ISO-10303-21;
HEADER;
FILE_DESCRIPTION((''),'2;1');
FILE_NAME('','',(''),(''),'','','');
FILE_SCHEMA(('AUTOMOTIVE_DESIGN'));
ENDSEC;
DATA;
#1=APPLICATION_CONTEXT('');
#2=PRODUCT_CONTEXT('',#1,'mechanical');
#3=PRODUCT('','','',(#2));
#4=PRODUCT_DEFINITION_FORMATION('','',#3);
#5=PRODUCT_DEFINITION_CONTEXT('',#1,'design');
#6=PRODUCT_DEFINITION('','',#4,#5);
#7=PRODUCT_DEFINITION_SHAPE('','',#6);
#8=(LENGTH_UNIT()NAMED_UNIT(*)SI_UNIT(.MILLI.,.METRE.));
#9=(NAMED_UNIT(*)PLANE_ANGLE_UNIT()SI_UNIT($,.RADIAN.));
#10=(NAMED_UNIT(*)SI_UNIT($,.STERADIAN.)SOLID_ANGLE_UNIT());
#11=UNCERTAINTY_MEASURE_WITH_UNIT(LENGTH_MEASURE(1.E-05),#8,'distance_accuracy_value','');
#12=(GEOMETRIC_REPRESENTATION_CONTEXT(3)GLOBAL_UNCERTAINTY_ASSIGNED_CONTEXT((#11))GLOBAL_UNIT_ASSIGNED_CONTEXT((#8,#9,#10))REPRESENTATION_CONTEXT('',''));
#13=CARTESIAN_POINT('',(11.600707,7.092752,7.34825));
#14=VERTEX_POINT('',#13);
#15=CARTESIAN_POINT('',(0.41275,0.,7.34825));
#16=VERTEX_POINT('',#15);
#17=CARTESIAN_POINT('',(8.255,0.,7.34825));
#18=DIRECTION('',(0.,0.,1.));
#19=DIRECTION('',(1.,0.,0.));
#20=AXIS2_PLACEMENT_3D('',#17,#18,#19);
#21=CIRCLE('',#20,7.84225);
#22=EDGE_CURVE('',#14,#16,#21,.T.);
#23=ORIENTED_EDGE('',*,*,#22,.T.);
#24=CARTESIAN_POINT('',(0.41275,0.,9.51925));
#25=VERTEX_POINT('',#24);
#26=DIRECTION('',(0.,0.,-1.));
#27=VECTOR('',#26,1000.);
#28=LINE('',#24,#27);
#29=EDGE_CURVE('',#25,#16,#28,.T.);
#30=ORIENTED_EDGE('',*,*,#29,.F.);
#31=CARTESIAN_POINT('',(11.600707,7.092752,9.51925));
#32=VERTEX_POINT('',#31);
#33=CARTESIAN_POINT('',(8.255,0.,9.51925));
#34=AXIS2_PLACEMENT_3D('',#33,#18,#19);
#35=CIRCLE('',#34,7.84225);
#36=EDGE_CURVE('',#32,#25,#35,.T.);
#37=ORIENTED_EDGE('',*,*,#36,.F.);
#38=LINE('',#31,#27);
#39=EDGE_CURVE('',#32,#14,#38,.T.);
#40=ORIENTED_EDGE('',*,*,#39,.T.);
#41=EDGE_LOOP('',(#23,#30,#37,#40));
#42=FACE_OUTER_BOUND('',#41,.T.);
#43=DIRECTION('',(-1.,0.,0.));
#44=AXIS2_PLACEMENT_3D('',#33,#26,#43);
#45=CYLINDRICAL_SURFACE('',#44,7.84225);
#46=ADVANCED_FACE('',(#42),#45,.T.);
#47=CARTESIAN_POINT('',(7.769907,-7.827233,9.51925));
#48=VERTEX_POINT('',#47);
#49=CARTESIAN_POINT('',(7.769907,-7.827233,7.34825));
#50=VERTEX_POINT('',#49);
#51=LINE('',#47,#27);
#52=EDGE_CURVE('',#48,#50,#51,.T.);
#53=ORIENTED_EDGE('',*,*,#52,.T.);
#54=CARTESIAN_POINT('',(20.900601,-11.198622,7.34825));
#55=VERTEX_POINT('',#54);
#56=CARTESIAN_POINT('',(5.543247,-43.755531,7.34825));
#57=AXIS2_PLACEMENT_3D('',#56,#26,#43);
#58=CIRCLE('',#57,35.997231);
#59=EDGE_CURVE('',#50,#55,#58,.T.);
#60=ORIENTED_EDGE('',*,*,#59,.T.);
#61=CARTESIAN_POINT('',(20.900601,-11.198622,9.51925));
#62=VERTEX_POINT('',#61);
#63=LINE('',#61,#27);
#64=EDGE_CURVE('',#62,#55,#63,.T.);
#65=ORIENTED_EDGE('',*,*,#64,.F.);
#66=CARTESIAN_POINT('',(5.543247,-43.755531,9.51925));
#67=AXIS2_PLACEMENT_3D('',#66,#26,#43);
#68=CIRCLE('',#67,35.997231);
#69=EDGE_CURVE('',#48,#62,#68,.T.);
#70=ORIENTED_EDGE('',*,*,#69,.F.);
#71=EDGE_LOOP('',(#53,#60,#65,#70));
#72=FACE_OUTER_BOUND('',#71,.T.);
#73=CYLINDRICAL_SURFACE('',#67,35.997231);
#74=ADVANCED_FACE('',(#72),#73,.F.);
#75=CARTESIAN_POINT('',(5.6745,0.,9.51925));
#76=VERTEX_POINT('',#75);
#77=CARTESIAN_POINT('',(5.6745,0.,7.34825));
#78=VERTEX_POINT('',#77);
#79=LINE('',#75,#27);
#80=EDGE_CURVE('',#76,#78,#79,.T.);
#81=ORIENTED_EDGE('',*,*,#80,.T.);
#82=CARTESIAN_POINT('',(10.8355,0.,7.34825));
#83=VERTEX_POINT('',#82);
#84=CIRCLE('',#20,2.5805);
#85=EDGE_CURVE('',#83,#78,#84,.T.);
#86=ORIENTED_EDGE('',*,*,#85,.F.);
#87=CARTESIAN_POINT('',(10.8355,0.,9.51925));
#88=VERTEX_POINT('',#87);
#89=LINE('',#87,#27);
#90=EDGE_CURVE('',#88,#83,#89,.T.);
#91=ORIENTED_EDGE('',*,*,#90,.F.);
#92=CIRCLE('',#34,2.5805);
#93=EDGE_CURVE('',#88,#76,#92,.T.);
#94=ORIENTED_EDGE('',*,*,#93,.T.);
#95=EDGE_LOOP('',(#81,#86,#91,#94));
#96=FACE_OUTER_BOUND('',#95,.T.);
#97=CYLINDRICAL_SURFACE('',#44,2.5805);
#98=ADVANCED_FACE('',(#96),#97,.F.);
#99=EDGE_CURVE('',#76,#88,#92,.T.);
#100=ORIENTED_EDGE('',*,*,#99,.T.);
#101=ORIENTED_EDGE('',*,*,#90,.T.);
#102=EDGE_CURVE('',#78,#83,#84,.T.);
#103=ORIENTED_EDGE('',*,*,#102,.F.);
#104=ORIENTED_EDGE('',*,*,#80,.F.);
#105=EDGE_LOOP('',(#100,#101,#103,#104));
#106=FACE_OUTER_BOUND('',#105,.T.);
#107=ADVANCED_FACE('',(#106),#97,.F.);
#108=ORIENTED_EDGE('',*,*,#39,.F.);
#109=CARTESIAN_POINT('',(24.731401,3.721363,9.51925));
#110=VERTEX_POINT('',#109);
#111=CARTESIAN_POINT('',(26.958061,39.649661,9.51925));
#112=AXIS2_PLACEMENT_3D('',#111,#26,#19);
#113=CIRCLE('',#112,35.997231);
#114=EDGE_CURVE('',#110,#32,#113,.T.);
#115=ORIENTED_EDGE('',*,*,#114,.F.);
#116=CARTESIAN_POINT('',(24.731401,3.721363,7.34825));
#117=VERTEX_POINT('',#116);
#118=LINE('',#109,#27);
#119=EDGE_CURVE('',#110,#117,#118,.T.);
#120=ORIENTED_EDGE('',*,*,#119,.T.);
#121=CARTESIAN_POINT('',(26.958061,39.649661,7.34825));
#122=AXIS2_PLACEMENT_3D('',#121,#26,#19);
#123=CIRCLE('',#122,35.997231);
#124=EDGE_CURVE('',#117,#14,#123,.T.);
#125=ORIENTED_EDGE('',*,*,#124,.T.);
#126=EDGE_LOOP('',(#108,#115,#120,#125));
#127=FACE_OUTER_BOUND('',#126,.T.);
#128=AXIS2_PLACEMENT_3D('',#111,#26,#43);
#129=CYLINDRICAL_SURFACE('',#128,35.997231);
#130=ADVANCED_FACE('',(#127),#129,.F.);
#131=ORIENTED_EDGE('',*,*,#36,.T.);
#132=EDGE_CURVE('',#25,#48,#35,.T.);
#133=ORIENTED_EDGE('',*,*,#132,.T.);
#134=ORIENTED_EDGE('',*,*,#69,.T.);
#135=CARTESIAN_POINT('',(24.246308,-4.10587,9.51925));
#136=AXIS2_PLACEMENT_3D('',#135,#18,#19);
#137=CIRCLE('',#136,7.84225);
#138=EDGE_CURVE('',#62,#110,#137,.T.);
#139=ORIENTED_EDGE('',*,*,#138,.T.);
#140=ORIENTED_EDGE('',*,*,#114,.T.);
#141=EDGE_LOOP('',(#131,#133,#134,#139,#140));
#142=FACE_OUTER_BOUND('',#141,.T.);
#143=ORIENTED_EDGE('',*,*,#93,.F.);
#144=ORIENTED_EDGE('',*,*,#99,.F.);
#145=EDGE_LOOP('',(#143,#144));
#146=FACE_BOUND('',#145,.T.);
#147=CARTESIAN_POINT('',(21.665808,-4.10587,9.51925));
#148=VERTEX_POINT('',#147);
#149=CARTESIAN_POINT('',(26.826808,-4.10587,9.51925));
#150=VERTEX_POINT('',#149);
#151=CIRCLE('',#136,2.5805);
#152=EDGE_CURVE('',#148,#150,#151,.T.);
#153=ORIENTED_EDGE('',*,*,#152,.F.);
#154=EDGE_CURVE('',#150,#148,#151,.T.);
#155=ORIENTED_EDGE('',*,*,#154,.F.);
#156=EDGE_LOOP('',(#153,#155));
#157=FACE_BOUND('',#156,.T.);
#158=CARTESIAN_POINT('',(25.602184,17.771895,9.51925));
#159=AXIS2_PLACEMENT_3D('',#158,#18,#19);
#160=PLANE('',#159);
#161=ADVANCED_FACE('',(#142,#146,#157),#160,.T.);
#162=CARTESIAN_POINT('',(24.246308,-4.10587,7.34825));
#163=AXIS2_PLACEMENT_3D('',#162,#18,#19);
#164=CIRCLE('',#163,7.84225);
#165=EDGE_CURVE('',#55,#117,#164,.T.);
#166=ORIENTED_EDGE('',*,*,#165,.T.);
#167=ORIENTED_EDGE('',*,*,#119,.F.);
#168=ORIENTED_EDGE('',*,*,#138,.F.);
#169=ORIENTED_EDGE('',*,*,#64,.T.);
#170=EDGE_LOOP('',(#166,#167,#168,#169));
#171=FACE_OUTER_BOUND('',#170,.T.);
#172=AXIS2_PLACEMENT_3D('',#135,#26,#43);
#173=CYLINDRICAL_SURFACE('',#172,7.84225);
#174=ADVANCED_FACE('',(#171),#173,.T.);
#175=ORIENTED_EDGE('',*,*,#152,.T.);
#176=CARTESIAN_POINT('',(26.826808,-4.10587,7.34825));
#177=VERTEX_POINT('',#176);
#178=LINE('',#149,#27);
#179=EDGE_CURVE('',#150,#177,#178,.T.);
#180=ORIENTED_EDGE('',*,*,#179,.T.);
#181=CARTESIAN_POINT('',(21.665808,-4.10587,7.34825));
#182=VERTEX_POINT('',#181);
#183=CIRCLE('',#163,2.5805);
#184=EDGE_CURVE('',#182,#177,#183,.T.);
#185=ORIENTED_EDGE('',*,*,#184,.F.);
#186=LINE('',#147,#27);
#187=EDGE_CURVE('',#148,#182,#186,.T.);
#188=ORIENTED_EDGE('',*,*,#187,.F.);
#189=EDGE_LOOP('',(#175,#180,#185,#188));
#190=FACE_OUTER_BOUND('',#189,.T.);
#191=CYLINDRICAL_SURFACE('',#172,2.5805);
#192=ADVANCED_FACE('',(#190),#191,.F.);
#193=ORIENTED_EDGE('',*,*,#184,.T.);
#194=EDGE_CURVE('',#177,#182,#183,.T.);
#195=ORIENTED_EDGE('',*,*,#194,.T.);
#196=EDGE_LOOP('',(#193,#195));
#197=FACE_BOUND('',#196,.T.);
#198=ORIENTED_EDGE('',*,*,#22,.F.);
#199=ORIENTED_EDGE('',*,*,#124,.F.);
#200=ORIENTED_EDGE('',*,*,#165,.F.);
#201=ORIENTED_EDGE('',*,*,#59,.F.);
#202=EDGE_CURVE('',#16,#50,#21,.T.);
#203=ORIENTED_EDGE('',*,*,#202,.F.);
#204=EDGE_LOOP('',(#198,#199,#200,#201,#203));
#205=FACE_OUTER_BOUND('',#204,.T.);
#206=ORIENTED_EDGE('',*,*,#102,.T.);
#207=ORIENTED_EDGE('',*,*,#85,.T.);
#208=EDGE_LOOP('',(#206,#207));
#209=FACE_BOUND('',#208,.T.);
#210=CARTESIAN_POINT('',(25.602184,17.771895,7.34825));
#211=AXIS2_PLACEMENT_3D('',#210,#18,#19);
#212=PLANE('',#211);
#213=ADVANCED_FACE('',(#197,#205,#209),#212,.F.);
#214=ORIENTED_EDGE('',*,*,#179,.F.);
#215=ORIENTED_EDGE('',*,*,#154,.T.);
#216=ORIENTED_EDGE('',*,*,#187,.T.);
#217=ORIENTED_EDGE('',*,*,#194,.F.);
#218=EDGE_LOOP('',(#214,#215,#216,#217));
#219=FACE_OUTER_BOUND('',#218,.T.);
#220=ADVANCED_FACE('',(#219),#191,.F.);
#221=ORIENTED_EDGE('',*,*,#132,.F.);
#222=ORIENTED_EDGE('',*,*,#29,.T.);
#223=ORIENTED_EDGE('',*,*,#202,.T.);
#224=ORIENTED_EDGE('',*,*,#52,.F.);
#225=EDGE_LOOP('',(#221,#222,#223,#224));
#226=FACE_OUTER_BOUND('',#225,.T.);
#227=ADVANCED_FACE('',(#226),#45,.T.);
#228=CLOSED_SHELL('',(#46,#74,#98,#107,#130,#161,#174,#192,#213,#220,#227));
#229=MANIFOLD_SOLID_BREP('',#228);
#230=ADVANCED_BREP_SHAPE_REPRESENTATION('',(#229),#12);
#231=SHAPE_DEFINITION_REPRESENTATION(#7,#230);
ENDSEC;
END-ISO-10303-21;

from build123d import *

# Parameters (mm, degrees)
SKETCH_2_R        = 7.94
EXTRUDE_1_DEPTH   = 7.875
EXTRUDE_1_2_DEPTH = 7.875
EXTRUDE_2_DEPTH   = 3.43
SKETCH_6_R        = 3.97
EXTRUDE_4_DEPTH   = 3.34
SCALE_1_SCALE     = 0.65


with BuildPart() as part:
    # 草图2 → 拉伸1 (new, symmetric)
    with BuildSketch(Plane.XY):
        with Locations((12.7, 0)):
            Circle(SKETCH_2_R)
    extrude(amount=EXTRUDE_1_DEPTH, both=True)



with BuildPart() as body_2:
    # 草图2 → Extrude 1 2 (new, symmetric)
    with BuildSketch(Plane.XY):
        with Locations((-12.7, 0)):
            Circle(SKETCH_2_R)
    extrude(amount=EXTRUDE_1_2_DEPTH, both=True)


with BuildPart() as part_1:
    add(part.part)

    add(body_2.part)  # 拉伸2 merges body 2
    # 草图3 → 拉伸2 (add)
    with BuildSketch(Plane.XY.offset(7.875)):
        with BuildLine():
            ThreePointArc((-10.428153415, 11.849174574), (-24.765, 0), (-10.428153415, -11.849174574))
            ThreePointArc((-10.428153415, -11.849174574), (0, -10.8585), (10.428153415, -11.849174574))
            ThreePointArc((10.428153415, -11.849174574), (24.765, 0), (10.428153415, 11.849174574))
            ThreePointArc((10.428153415, 11.849174574), (0, 10.8585), (-10.428153415, 11.849174574))
        make_face()
    extrude(amount=EXTRUDE_2_DEPTH)


with BuildPart() as body_2_2:
    # 草图6 → 拉伸4 (new body)
    with BuildSketch(Plane.XY.offset(11.305)):
        with BuildLine():
            ThreePointArc((32.154770058, -17.228648829), (48.987968132, -9.317166623), (38.048309834, 5.725173103))
            ThreePointArc((38.048309834, 5.725173103), (27.701405286, 7.358998688), (17.847242234, 10.911925695))
            ThreePointArc((17.847242234, 10.911925695), (1.014044161, 3.000443489), (11.953702459, -12.041896237))
            ThreePointArc((11.953702459, -12.041896237), (22.300607007, -13.675721822), (32.154770058, -17.228648829))
        make_face()
        with Locations((12.7, 0)):
            Circle(SKETCH_6_R, mode=Mode.SUBTRACT)
        with Locations((37.302012293, -6.316723134)):
            Circle(SKETCH_6_R, mode=Mode.SUBTRACT)
    extrude(amount=EXTRUDE_4_DEPTH)


with BuildPart() as body_2_2_1:
    # 缩放比例1: scaled about (0, 0, 0)
    add(body_2_2.part.scale(SCALE_1_SCALE))


solid = body_2_2_1.part
